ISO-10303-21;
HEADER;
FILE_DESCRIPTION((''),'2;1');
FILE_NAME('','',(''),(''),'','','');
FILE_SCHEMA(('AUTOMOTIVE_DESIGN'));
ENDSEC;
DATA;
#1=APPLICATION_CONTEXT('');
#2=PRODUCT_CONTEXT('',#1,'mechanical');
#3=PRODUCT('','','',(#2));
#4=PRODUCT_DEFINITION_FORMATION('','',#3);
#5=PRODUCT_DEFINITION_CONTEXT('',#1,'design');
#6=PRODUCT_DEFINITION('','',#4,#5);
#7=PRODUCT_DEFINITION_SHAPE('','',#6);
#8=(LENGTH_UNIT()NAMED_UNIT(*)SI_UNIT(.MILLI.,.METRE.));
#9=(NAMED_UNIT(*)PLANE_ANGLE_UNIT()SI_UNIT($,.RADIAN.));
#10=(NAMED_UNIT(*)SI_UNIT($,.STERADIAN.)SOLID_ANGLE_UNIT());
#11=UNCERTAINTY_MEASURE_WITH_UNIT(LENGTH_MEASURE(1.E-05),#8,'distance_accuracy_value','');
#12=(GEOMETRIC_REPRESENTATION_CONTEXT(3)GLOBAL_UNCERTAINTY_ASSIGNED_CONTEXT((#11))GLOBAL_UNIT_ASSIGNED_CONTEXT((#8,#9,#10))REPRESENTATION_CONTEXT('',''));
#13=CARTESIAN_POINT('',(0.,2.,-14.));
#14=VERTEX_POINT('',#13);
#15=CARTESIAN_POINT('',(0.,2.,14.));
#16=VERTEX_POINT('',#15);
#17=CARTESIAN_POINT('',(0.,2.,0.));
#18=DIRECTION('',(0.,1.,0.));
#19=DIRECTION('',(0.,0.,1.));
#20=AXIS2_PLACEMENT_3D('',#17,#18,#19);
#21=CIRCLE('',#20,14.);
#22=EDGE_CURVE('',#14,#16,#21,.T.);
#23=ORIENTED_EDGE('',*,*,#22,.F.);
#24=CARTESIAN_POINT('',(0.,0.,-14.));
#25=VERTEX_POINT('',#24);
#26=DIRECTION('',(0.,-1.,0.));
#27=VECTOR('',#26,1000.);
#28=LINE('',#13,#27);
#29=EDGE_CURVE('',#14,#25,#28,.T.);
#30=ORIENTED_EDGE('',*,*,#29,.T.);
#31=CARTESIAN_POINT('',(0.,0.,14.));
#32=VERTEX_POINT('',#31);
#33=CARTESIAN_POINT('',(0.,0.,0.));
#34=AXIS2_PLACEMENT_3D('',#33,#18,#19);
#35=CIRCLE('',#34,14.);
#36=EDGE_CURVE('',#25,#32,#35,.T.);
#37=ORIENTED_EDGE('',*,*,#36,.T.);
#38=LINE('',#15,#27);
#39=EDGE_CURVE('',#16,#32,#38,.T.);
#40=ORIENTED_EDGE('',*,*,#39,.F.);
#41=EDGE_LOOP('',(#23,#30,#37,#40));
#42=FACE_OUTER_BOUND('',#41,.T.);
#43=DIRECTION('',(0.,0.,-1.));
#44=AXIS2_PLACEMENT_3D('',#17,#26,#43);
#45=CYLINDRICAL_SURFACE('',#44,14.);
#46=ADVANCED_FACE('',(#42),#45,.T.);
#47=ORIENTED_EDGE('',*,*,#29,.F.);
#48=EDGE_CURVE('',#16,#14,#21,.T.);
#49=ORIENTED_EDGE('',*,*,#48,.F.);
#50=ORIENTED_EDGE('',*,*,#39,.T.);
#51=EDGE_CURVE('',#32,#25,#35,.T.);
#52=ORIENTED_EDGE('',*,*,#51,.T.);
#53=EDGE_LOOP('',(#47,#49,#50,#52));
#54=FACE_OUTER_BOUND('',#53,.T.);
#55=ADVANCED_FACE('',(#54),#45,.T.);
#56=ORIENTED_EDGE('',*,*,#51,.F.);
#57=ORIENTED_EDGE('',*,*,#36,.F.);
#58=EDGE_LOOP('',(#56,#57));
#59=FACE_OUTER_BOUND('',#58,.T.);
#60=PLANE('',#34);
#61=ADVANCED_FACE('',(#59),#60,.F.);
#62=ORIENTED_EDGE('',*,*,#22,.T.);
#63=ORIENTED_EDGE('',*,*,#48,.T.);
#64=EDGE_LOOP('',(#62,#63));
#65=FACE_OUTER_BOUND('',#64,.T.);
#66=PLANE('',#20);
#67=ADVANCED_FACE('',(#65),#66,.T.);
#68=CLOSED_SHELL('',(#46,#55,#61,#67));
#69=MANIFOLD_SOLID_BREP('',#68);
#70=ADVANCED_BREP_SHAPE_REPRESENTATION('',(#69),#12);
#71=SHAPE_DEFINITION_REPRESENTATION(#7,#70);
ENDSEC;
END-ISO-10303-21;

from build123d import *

# Parameters (mm, degrees)
SKETCH1_R           = 14
BOSS_EXTRUDE1_DEPTH = 2


with BuildPart() as part:
    # Sketch1 → Boss-Extrude1 (new body)
    with BuildSketch(Plane(origin=(0, 0, 0), x_dir=(1, 0, 0), z_dir=(0, 1, 0))):
        with Locations(Location((0, 0, 0), (0, 0, 270))):
            Circle(SKETCH1_R)
    extrude(amount=BOSS_EXTRUDE1_DEPTH)


solid = part.part
